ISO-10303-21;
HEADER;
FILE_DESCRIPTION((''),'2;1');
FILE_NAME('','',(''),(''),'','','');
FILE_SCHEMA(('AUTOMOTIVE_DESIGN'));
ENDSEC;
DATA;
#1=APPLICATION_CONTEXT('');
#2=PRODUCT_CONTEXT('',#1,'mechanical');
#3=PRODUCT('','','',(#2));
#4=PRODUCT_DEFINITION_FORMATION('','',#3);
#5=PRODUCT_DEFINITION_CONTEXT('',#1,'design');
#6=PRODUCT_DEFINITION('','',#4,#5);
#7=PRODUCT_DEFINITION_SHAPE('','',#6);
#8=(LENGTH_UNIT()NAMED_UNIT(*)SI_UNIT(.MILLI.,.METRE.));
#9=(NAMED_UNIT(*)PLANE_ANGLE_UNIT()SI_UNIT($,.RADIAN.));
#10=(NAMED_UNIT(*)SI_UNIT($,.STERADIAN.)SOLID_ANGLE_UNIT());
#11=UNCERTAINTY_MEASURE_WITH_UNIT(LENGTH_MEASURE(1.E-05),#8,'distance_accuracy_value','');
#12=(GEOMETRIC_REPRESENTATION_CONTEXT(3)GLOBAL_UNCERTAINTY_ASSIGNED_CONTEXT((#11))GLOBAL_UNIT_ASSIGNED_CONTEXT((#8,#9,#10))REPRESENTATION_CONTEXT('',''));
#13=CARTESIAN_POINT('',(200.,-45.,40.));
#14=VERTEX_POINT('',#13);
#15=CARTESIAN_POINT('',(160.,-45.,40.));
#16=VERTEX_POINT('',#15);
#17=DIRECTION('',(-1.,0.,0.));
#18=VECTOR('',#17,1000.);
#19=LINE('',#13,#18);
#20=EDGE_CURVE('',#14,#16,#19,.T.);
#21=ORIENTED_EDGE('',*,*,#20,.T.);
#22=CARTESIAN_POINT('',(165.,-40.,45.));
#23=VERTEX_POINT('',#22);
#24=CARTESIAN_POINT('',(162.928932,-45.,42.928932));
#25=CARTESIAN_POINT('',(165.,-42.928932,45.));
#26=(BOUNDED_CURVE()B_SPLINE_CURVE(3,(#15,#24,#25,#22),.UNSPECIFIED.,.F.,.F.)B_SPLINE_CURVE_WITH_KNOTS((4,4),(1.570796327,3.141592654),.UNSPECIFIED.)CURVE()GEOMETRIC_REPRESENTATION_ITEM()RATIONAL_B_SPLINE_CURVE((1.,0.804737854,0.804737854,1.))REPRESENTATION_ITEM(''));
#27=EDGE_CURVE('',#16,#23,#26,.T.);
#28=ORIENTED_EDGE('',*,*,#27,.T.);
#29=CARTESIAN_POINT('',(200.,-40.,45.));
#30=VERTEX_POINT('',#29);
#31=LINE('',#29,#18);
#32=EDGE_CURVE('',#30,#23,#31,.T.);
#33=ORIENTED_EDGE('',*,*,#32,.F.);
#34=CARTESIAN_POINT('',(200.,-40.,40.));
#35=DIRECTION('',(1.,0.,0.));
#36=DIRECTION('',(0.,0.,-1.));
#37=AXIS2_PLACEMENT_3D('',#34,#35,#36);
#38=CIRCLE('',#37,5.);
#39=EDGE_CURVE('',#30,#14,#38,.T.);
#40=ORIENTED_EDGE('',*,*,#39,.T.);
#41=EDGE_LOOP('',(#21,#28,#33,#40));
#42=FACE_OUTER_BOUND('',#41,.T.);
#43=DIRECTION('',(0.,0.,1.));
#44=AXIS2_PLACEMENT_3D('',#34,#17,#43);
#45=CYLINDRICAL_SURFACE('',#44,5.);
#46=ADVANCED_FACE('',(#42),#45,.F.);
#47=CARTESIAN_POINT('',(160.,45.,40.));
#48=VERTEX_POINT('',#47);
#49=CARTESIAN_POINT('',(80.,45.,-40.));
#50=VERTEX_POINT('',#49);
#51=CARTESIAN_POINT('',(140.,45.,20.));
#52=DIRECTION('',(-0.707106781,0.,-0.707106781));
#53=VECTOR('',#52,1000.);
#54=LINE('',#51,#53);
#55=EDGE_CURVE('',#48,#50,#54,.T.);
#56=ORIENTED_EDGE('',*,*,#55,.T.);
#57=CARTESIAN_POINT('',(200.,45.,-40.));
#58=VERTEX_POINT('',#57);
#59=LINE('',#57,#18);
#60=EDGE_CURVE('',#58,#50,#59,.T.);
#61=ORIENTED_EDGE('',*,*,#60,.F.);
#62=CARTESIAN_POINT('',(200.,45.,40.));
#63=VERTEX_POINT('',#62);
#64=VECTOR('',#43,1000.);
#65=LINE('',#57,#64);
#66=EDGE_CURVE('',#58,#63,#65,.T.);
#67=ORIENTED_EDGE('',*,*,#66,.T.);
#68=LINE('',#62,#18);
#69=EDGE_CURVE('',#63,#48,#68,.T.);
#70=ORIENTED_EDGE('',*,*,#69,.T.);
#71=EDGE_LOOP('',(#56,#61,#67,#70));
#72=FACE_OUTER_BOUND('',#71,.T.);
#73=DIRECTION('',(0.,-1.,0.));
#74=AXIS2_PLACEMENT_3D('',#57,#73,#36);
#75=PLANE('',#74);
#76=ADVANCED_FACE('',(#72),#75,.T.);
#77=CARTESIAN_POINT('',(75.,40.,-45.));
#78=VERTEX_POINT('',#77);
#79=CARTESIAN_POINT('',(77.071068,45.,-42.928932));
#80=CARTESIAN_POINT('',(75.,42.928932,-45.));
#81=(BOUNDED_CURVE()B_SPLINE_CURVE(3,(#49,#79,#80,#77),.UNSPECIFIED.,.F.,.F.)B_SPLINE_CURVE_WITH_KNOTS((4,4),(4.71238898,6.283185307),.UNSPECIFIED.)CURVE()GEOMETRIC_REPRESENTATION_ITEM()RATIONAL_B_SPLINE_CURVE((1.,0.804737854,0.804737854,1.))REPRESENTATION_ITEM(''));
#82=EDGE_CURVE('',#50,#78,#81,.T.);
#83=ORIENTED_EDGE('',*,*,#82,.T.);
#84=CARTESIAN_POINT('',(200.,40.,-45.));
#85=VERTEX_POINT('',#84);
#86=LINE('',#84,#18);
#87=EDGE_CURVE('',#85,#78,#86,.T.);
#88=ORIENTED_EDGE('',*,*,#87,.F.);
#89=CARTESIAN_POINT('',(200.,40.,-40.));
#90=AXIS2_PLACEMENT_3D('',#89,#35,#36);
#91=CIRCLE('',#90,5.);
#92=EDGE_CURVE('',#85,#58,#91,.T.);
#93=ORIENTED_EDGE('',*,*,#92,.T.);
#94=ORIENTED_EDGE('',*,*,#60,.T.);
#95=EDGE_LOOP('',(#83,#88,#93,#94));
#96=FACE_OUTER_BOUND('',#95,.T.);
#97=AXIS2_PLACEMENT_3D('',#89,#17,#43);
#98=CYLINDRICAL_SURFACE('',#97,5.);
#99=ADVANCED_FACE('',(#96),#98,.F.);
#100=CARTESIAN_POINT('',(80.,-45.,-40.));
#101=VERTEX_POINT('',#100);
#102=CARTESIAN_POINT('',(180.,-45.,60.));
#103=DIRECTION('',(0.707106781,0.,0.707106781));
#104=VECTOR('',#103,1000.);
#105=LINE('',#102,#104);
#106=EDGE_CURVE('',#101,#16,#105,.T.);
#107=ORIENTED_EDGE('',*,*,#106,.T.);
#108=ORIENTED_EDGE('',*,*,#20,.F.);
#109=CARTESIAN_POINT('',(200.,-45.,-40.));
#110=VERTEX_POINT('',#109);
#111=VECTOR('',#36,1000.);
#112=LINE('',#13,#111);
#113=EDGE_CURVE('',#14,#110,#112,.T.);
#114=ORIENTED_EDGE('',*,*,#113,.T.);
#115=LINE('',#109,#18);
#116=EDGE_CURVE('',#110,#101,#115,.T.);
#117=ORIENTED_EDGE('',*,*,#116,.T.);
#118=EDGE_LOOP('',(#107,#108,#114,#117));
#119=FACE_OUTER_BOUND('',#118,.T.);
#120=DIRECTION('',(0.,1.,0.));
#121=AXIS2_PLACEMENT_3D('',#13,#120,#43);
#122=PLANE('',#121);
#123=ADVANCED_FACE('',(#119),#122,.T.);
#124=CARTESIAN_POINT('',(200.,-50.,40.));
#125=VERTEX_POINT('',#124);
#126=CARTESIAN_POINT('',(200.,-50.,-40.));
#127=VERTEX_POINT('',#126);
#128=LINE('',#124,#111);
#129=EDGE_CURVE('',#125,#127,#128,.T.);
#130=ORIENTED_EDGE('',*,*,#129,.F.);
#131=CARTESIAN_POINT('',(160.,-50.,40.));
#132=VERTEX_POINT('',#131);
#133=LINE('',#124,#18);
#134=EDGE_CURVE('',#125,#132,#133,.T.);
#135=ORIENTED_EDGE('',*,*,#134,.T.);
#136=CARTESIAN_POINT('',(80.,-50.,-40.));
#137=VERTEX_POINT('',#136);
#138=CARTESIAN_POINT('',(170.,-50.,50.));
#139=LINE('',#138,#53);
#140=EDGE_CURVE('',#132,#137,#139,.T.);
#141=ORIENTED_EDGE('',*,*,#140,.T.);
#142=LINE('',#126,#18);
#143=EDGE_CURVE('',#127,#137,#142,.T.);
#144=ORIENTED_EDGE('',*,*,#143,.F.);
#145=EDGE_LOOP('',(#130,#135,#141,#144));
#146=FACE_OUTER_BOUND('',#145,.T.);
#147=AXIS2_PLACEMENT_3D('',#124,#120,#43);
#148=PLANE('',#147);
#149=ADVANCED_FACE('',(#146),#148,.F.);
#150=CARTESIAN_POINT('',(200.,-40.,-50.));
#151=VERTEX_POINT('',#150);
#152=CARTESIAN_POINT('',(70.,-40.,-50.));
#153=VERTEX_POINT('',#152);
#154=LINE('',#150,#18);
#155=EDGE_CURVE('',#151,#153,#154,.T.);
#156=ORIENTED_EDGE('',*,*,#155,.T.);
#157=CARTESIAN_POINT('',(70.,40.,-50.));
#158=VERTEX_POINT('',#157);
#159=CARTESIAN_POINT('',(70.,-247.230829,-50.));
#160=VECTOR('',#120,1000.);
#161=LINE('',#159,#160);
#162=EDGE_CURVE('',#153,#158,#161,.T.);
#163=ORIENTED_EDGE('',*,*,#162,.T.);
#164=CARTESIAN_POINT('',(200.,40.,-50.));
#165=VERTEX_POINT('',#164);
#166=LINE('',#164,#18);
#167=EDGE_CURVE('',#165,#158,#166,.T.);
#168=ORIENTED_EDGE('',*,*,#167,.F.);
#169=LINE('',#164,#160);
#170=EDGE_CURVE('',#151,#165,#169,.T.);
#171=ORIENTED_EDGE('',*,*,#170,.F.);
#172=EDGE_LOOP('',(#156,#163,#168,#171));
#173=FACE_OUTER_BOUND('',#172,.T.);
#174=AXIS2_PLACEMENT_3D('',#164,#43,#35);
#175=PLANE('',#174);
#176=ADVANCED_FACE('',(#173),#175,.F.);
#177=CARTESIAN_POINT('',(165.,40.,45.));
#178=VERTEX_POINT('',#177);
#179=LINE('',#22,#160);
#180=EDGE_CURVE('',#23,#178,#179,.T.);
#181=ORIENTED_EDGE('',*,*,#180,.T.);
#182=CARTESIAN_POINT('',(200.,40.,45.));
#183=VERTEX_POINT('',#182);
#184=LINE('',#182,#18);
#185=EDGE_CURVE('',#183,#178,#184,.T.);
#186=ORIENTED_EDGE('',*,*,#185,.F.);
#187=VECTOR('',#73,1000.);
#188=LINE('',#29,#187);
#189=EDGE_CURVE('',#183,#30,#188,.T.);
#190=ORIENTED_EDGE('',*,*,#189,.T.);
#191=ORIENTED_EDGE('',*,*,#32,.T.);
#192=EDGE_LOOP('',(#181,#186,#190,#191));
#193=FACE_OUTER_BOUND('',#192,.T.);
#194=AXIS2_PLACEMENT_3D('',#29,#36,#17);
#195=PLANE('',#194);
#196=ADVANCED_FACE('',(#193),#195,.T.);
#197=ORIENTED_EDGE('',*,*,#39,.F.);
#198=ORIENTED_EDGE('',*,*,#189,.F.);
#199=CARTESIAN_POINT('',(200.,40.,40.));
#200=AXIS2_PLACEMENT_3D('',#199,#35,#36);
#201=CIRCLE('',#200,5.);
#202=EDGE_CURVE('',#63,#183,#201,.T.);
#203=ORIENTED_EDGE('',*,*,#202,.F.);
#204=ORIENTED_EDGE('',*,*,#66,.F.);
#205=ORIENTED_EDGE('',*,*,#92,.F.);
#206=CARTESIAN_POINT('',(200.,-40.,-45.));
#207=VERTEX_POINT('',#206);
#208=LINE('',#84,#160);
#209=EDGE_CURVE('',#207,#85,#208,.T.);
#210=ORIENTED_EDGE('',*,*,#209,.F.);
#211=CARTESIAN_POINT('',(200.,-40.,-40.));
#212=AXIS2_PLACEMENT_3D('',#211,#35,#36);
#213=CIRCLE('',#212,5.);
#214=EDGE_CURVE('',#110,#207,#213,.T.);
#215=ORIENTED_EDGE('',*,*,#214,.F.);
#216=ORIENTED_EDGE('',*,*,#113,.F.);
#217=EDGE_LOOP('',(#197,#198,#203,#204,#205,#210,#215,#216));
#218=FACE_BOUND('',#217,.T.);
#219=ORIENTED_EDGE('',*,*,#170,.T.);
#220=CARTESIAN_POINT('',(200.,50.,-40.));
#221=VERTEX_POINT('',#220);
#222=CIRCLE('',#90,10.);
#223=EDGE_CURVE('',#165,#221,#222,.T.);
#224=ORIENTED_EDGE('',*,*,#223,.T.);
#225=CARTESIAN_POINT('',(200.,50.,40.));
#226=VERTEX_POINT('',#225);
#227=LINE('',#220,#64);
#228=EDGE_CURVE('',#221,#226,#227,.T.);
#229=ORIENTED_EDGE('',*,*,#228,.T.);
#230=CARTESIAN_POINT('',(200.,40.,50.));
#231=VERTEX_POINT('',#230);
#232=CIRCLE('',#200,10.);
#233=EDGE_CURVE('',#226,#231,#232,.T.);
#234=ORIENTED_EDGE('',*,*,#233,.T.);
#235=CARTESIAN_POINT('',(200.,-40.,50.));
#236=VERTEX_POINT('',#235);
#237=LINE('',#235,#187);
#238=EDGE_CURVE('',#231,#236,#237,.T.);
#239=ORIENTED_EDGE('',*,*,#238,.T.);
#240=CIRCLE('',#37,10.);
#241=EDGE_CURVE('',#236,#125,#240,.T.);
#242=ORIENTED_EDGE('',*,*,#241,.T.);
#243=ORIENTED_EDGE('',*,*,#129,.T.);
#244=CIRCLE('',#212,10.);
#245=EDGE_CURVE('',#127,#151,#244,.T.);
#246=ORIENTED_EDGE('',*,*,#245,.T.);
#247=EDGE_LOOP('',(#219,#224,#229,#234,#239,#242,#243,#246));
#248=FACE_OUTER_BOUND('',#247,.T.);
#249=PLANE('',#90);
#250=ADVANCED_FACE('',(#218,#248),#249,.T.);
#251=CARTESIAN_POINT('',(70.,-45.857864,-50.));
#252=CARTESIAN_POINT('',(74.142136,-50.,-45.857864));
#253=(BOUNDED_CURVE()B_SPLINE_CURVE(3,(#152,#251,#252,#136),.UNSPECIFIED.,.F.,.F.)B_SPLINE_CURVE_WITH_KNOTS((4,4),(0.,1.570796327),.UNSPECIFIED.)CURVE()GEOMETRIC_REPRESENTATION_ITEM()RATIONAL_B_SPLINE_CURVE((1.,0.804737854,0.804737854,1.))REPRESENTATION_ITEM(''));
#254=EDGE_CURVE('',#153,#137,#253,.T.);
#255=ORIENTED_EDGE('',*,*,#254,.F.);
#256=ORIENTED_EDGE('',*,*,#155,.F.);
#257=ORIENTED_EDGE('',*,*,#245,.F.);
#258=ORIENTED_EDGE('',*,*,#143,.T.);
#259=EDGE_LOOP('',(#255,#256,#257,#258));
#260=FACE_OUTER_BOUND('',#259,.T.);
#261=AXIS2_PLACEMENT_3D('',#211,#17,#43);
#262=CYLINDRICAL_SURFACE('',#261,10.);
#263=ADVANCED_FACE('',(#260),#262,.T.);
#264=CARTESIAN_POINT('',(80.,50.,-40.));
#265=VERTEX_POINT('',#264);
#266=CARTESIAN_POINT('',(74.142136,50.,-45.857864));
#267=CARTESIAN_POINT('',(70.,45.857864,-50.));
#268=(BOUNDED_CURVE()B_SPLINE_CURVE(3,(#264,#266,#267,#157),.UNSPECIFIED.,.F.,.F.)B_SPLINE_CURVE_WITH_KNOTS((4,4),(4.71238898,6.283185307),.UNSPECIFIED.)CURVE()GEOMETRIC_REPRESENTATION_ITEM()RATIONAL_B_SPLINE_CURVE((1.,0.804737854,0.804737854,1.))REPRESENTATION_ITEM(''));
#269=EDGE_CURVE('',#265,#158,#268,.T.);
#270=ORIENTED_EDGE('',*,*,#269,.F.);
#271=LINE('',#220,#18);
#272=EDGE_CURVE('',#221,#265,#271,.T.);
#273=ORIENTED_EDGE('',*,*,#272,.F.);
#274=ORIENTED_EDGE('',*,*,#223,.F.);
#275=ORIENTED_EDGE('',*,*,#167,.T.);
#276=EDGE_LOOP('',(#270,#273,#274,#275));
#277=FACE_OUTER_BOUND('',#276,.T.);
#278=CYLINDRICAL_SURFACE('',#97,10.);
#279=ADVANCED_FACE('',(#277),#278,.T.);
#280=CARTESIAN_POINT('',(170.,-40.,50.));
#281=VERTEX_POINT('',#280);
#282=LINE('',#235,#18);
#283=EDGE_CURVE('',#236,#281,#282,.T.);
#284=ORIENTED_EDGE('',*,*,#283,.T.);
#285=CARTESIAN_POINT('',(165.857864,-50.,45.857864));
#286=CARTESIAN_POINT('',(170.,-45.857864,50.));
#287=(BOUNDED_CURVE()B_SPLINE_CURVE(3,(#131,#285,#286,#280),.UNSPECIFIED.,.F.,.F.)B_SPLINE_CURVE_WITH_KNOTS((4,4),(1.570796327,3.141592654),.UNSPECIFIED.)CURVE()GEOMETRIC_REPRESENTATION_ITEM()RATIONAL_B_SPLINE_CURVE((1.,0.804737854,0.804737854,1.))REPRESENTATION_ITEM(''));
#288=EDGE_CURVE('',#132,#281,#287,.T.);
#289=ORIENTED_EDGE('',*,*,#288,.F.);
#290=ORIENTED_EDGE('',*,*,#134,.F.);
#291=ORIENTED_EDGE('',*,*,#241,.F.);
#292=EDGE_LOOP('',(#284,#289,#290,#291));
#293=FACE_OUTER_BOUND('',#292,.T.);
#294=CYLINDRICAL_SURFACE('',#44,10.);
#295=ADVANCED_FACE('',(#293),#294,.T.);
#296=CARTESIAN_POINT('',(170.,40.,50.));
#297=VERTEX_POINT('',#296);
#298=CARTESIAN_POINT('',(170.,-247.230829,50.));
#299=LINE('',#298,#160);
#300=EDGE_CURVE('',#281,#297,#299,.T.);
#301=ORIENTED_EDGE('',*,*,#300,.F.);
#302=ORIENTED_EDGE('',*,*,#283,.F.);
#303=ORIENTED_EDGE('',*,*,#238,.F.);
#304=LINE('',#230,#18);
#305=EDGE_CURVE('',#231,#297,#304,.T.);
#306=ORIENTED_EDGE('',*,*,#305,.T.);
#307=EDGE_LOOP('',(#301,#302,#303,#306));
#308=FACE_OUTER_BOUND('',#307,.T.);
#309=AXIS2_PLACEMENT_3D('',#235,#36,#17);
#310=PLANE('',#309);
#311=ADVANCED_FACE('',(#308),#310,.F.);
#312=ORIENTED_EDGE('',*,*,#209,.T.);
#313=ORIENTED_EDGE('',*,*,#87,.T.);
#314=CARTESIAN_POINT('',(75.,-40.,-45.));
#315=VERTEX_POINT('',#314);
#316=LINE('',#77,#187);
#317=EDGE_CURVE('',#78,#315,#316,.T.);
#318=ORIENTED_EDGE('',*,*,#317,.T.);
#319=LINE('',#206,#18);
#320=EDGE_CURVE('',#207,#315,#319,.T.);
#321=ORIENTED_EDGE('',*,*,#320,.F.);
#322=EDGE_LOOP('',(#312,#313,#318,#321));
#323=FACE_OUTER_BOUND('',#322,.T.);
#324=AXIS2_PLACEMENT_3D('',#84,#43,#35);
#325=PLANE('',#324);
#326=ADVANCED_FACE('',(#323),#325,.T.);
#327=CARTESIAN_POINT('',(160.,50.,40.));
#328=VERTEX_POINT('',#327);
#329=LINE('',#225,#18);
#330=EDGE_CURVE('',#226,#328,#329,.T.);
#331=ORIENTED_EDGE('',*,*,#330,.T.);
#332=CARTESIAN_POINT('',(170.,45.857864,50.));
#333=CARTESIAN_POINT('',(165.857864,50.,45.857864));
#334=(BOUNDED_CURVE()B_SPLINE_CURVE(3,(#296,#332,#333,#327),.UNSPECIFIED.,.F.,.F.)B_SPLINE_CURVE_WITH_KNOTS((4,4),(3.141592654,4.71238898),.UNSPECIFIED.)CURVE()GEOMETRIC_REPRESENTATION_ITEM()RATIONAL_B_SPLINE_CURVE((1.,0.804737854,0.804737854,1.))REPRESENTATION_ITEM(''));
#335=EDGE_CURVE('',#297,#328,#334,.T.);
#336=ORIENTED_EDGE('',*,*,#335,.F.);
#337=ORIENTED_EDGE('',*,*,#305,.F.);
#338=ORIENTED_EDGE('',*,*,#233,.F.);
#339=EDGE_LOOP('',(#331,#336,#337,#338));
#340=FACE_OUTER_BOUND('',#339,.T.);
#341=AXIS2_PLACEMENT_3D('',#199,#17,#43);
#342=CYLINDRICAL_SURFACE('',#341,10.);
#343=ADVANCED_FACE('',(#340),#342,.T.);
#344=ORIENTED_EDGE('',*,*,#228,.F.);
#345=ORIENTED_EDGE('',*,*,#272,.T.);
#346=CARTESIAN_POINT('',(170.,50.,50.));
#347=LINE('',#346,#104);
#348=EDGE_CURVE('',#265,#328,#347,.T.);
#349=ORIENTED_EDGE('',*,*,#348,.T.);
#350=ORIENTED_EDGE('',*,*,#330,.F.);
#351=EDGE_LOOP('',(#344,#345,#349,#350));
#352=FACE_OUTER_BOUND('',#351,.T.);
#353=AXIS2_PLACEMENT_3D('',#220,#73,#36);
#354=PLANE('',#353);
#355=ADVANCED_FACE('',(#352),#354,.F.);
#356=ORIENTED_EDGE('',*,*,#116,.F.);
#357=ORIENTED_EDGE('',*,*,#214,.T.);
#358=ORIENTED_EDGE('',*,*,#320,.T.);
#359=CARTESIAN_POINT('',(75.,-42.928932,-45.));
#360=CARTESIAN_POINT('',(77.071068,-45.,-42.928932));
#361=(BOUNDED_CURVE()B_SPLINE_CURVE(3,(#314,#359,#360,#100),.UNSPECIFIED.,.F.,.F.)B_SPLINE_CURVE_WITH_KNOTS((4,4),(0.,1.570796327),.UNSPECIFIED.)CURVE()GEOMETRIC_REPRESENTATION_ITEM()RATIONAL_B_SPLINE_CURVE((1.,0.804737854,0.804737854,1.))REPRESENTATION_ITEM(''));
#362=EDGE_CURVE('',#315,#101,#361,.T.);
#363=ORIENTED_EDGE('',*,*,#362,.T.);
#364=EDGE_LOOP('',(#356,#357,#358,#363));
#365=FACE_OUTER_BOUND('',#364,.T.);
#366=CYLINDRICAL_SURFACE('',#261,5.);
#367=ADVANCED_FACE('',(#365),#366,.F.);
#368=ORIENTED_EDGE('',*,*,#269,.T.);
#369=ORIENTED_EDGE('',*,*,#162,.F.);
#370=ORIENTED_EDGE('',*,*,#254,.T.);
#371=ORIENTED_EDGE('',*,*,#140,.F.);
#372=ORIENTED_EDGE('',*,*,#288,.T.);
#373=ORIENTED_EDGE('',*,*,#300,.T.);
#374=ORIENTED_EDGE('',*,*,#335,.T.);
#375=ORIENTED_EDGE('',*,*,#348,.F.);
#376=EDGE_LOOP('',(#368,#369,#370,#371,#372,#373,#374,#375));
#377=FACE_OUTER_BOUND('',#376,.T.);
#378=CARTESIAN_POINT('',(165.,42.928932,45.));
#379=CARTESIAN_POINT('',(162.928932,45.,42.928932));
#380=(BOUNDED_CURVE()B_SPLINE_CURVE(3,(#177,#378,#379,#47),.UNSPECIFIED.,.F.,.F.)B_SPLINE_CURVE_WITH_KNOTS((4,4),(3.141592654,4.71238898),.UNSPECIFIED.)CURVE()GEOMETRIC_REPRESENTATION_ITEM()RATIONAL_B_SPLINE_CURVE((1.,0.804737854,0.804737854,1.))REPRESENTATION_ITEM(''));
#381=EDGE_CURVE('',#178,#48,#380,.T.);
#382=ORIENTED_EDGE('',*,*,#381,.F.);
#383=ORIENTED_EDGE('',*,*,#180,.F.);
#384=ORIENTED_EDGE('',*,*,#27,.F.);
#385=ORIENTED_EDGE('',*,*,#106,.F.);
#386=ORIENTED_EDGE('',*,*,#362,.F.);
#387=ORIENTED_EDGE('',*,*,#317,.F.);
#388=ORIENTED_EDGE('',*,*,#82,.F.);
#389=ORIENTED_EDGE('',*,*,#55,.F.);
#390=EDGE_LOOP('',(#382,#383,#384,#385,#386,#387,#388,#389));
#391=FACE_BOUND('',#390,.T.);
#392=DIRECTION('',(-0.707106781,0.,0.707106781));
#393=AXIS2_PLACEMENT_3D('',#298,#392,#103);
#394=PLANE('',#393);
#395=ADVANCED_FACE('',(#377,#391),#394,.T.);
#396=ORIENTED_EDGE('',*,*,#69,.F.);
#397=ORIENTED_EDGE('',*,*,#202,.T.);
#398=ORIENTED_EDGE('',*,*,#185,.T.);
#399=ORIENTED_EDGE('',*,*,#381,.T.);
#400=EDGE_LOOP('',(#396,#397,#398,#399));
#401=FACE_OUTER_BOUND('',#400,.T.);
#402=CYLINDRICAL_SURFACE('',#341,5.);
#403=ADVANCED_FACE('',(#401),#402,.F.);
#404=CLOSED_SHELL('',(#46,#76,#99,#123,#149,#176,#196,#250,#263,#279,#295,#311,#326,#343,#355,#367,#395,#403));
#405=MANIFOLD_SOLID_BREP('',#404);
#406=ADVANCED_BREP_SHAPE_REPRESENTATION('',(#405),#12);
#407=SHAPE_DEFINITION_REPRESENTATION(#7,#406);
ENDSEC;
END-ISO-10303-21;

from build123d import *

# Parameters (mm, degrees)
F_100_X_100_X_5_1_DEPTH = 200
CUT_EXTRUDE_1_REACH     = 231.129


with BuildPart() as part:
    # Sketch1 → 方形管 100 X 100 X 5   (1) (new body)
    with BuildSketch(Plane(origin=(0, 0, 0), x_dir=(0, 0, -1), z_dir=(1, 0, 0))):
        with BuildLine():
            Line((-40, -50), (40, -50))
            ThreePointArc((40, -50), (47.071067812, -47.071067812), (50, -40))
            Line((50, -40), (50, 40))
            ThreePointArc((50, 40), (47.071067812, 47.071067812), (40, 50))
            Line((40, 50), (-40, 50))
            ThreePointArc((-40, 50), (-47.071067812, 47.071067812), (-50, 40))
            Line((-50, 40), (-50, -40))
            ThreePointArc((-50, -40), (-47.071067812, -47.071067812), (-40, -50))
        make_face()
        with BuildLine():
            Line((-40, -45), (40, -45))
            ThreePointArc((40, -45), (43.535533906, -43.535533906), (45, -40))
            Line((45, -40), (45, 40))
            ThreePointArc((45, 40), (43.535533906, 43.535533906), (40, 45))
            Line((40, 45), (-40, 45))
            ThreePointArc((-40, 45), (-43.535533906, 43.535533906), (-45, 40))
            Line((-45, 40), (-45, -40))
            ThreePointArc((-45, -40), (-43.535533906, -43.535533906), (-40, -45))
        make_face(mode=Mode.SUBTRACT)
    extrude(amount=F_100_X_100_X_5_1_DEPTH)

    # 切除-拉伸1: up to this face of the body (flat: up to its plane)
    cut_extrude_1_end = Plane(part.part.faces().sort_by_distance((100, -50, 0))[0])
    # 草图2 → 切除-拉伸1 (cut, up to the picked face)
    with BuildSketch(Plane.XZ.offset(-50), mode=Mode.PRIVATE) as cut_extrude_1_sk1:
        Polygon((170, 50), (70, -50), (0, -50), (0, 50), align=None)
    cut_extrude_1_tool1 = split(extrude(cut_extrude_1_sk1.sketch, amount=CUT_EXTRUDE_1_REACH, mode=Mode.PRIVATE), bisect_by=cut_extrude_1_end, keep=Keep.BOTH, mode=Mode.PRIVATE)
    add(cut_extrude_1_tool1.solids().sort_by(Axis((63.472222, 50, 6.944444), (0, -1, 0)))[0], mode=Mode.SUBTRACT)


solid = part.part
